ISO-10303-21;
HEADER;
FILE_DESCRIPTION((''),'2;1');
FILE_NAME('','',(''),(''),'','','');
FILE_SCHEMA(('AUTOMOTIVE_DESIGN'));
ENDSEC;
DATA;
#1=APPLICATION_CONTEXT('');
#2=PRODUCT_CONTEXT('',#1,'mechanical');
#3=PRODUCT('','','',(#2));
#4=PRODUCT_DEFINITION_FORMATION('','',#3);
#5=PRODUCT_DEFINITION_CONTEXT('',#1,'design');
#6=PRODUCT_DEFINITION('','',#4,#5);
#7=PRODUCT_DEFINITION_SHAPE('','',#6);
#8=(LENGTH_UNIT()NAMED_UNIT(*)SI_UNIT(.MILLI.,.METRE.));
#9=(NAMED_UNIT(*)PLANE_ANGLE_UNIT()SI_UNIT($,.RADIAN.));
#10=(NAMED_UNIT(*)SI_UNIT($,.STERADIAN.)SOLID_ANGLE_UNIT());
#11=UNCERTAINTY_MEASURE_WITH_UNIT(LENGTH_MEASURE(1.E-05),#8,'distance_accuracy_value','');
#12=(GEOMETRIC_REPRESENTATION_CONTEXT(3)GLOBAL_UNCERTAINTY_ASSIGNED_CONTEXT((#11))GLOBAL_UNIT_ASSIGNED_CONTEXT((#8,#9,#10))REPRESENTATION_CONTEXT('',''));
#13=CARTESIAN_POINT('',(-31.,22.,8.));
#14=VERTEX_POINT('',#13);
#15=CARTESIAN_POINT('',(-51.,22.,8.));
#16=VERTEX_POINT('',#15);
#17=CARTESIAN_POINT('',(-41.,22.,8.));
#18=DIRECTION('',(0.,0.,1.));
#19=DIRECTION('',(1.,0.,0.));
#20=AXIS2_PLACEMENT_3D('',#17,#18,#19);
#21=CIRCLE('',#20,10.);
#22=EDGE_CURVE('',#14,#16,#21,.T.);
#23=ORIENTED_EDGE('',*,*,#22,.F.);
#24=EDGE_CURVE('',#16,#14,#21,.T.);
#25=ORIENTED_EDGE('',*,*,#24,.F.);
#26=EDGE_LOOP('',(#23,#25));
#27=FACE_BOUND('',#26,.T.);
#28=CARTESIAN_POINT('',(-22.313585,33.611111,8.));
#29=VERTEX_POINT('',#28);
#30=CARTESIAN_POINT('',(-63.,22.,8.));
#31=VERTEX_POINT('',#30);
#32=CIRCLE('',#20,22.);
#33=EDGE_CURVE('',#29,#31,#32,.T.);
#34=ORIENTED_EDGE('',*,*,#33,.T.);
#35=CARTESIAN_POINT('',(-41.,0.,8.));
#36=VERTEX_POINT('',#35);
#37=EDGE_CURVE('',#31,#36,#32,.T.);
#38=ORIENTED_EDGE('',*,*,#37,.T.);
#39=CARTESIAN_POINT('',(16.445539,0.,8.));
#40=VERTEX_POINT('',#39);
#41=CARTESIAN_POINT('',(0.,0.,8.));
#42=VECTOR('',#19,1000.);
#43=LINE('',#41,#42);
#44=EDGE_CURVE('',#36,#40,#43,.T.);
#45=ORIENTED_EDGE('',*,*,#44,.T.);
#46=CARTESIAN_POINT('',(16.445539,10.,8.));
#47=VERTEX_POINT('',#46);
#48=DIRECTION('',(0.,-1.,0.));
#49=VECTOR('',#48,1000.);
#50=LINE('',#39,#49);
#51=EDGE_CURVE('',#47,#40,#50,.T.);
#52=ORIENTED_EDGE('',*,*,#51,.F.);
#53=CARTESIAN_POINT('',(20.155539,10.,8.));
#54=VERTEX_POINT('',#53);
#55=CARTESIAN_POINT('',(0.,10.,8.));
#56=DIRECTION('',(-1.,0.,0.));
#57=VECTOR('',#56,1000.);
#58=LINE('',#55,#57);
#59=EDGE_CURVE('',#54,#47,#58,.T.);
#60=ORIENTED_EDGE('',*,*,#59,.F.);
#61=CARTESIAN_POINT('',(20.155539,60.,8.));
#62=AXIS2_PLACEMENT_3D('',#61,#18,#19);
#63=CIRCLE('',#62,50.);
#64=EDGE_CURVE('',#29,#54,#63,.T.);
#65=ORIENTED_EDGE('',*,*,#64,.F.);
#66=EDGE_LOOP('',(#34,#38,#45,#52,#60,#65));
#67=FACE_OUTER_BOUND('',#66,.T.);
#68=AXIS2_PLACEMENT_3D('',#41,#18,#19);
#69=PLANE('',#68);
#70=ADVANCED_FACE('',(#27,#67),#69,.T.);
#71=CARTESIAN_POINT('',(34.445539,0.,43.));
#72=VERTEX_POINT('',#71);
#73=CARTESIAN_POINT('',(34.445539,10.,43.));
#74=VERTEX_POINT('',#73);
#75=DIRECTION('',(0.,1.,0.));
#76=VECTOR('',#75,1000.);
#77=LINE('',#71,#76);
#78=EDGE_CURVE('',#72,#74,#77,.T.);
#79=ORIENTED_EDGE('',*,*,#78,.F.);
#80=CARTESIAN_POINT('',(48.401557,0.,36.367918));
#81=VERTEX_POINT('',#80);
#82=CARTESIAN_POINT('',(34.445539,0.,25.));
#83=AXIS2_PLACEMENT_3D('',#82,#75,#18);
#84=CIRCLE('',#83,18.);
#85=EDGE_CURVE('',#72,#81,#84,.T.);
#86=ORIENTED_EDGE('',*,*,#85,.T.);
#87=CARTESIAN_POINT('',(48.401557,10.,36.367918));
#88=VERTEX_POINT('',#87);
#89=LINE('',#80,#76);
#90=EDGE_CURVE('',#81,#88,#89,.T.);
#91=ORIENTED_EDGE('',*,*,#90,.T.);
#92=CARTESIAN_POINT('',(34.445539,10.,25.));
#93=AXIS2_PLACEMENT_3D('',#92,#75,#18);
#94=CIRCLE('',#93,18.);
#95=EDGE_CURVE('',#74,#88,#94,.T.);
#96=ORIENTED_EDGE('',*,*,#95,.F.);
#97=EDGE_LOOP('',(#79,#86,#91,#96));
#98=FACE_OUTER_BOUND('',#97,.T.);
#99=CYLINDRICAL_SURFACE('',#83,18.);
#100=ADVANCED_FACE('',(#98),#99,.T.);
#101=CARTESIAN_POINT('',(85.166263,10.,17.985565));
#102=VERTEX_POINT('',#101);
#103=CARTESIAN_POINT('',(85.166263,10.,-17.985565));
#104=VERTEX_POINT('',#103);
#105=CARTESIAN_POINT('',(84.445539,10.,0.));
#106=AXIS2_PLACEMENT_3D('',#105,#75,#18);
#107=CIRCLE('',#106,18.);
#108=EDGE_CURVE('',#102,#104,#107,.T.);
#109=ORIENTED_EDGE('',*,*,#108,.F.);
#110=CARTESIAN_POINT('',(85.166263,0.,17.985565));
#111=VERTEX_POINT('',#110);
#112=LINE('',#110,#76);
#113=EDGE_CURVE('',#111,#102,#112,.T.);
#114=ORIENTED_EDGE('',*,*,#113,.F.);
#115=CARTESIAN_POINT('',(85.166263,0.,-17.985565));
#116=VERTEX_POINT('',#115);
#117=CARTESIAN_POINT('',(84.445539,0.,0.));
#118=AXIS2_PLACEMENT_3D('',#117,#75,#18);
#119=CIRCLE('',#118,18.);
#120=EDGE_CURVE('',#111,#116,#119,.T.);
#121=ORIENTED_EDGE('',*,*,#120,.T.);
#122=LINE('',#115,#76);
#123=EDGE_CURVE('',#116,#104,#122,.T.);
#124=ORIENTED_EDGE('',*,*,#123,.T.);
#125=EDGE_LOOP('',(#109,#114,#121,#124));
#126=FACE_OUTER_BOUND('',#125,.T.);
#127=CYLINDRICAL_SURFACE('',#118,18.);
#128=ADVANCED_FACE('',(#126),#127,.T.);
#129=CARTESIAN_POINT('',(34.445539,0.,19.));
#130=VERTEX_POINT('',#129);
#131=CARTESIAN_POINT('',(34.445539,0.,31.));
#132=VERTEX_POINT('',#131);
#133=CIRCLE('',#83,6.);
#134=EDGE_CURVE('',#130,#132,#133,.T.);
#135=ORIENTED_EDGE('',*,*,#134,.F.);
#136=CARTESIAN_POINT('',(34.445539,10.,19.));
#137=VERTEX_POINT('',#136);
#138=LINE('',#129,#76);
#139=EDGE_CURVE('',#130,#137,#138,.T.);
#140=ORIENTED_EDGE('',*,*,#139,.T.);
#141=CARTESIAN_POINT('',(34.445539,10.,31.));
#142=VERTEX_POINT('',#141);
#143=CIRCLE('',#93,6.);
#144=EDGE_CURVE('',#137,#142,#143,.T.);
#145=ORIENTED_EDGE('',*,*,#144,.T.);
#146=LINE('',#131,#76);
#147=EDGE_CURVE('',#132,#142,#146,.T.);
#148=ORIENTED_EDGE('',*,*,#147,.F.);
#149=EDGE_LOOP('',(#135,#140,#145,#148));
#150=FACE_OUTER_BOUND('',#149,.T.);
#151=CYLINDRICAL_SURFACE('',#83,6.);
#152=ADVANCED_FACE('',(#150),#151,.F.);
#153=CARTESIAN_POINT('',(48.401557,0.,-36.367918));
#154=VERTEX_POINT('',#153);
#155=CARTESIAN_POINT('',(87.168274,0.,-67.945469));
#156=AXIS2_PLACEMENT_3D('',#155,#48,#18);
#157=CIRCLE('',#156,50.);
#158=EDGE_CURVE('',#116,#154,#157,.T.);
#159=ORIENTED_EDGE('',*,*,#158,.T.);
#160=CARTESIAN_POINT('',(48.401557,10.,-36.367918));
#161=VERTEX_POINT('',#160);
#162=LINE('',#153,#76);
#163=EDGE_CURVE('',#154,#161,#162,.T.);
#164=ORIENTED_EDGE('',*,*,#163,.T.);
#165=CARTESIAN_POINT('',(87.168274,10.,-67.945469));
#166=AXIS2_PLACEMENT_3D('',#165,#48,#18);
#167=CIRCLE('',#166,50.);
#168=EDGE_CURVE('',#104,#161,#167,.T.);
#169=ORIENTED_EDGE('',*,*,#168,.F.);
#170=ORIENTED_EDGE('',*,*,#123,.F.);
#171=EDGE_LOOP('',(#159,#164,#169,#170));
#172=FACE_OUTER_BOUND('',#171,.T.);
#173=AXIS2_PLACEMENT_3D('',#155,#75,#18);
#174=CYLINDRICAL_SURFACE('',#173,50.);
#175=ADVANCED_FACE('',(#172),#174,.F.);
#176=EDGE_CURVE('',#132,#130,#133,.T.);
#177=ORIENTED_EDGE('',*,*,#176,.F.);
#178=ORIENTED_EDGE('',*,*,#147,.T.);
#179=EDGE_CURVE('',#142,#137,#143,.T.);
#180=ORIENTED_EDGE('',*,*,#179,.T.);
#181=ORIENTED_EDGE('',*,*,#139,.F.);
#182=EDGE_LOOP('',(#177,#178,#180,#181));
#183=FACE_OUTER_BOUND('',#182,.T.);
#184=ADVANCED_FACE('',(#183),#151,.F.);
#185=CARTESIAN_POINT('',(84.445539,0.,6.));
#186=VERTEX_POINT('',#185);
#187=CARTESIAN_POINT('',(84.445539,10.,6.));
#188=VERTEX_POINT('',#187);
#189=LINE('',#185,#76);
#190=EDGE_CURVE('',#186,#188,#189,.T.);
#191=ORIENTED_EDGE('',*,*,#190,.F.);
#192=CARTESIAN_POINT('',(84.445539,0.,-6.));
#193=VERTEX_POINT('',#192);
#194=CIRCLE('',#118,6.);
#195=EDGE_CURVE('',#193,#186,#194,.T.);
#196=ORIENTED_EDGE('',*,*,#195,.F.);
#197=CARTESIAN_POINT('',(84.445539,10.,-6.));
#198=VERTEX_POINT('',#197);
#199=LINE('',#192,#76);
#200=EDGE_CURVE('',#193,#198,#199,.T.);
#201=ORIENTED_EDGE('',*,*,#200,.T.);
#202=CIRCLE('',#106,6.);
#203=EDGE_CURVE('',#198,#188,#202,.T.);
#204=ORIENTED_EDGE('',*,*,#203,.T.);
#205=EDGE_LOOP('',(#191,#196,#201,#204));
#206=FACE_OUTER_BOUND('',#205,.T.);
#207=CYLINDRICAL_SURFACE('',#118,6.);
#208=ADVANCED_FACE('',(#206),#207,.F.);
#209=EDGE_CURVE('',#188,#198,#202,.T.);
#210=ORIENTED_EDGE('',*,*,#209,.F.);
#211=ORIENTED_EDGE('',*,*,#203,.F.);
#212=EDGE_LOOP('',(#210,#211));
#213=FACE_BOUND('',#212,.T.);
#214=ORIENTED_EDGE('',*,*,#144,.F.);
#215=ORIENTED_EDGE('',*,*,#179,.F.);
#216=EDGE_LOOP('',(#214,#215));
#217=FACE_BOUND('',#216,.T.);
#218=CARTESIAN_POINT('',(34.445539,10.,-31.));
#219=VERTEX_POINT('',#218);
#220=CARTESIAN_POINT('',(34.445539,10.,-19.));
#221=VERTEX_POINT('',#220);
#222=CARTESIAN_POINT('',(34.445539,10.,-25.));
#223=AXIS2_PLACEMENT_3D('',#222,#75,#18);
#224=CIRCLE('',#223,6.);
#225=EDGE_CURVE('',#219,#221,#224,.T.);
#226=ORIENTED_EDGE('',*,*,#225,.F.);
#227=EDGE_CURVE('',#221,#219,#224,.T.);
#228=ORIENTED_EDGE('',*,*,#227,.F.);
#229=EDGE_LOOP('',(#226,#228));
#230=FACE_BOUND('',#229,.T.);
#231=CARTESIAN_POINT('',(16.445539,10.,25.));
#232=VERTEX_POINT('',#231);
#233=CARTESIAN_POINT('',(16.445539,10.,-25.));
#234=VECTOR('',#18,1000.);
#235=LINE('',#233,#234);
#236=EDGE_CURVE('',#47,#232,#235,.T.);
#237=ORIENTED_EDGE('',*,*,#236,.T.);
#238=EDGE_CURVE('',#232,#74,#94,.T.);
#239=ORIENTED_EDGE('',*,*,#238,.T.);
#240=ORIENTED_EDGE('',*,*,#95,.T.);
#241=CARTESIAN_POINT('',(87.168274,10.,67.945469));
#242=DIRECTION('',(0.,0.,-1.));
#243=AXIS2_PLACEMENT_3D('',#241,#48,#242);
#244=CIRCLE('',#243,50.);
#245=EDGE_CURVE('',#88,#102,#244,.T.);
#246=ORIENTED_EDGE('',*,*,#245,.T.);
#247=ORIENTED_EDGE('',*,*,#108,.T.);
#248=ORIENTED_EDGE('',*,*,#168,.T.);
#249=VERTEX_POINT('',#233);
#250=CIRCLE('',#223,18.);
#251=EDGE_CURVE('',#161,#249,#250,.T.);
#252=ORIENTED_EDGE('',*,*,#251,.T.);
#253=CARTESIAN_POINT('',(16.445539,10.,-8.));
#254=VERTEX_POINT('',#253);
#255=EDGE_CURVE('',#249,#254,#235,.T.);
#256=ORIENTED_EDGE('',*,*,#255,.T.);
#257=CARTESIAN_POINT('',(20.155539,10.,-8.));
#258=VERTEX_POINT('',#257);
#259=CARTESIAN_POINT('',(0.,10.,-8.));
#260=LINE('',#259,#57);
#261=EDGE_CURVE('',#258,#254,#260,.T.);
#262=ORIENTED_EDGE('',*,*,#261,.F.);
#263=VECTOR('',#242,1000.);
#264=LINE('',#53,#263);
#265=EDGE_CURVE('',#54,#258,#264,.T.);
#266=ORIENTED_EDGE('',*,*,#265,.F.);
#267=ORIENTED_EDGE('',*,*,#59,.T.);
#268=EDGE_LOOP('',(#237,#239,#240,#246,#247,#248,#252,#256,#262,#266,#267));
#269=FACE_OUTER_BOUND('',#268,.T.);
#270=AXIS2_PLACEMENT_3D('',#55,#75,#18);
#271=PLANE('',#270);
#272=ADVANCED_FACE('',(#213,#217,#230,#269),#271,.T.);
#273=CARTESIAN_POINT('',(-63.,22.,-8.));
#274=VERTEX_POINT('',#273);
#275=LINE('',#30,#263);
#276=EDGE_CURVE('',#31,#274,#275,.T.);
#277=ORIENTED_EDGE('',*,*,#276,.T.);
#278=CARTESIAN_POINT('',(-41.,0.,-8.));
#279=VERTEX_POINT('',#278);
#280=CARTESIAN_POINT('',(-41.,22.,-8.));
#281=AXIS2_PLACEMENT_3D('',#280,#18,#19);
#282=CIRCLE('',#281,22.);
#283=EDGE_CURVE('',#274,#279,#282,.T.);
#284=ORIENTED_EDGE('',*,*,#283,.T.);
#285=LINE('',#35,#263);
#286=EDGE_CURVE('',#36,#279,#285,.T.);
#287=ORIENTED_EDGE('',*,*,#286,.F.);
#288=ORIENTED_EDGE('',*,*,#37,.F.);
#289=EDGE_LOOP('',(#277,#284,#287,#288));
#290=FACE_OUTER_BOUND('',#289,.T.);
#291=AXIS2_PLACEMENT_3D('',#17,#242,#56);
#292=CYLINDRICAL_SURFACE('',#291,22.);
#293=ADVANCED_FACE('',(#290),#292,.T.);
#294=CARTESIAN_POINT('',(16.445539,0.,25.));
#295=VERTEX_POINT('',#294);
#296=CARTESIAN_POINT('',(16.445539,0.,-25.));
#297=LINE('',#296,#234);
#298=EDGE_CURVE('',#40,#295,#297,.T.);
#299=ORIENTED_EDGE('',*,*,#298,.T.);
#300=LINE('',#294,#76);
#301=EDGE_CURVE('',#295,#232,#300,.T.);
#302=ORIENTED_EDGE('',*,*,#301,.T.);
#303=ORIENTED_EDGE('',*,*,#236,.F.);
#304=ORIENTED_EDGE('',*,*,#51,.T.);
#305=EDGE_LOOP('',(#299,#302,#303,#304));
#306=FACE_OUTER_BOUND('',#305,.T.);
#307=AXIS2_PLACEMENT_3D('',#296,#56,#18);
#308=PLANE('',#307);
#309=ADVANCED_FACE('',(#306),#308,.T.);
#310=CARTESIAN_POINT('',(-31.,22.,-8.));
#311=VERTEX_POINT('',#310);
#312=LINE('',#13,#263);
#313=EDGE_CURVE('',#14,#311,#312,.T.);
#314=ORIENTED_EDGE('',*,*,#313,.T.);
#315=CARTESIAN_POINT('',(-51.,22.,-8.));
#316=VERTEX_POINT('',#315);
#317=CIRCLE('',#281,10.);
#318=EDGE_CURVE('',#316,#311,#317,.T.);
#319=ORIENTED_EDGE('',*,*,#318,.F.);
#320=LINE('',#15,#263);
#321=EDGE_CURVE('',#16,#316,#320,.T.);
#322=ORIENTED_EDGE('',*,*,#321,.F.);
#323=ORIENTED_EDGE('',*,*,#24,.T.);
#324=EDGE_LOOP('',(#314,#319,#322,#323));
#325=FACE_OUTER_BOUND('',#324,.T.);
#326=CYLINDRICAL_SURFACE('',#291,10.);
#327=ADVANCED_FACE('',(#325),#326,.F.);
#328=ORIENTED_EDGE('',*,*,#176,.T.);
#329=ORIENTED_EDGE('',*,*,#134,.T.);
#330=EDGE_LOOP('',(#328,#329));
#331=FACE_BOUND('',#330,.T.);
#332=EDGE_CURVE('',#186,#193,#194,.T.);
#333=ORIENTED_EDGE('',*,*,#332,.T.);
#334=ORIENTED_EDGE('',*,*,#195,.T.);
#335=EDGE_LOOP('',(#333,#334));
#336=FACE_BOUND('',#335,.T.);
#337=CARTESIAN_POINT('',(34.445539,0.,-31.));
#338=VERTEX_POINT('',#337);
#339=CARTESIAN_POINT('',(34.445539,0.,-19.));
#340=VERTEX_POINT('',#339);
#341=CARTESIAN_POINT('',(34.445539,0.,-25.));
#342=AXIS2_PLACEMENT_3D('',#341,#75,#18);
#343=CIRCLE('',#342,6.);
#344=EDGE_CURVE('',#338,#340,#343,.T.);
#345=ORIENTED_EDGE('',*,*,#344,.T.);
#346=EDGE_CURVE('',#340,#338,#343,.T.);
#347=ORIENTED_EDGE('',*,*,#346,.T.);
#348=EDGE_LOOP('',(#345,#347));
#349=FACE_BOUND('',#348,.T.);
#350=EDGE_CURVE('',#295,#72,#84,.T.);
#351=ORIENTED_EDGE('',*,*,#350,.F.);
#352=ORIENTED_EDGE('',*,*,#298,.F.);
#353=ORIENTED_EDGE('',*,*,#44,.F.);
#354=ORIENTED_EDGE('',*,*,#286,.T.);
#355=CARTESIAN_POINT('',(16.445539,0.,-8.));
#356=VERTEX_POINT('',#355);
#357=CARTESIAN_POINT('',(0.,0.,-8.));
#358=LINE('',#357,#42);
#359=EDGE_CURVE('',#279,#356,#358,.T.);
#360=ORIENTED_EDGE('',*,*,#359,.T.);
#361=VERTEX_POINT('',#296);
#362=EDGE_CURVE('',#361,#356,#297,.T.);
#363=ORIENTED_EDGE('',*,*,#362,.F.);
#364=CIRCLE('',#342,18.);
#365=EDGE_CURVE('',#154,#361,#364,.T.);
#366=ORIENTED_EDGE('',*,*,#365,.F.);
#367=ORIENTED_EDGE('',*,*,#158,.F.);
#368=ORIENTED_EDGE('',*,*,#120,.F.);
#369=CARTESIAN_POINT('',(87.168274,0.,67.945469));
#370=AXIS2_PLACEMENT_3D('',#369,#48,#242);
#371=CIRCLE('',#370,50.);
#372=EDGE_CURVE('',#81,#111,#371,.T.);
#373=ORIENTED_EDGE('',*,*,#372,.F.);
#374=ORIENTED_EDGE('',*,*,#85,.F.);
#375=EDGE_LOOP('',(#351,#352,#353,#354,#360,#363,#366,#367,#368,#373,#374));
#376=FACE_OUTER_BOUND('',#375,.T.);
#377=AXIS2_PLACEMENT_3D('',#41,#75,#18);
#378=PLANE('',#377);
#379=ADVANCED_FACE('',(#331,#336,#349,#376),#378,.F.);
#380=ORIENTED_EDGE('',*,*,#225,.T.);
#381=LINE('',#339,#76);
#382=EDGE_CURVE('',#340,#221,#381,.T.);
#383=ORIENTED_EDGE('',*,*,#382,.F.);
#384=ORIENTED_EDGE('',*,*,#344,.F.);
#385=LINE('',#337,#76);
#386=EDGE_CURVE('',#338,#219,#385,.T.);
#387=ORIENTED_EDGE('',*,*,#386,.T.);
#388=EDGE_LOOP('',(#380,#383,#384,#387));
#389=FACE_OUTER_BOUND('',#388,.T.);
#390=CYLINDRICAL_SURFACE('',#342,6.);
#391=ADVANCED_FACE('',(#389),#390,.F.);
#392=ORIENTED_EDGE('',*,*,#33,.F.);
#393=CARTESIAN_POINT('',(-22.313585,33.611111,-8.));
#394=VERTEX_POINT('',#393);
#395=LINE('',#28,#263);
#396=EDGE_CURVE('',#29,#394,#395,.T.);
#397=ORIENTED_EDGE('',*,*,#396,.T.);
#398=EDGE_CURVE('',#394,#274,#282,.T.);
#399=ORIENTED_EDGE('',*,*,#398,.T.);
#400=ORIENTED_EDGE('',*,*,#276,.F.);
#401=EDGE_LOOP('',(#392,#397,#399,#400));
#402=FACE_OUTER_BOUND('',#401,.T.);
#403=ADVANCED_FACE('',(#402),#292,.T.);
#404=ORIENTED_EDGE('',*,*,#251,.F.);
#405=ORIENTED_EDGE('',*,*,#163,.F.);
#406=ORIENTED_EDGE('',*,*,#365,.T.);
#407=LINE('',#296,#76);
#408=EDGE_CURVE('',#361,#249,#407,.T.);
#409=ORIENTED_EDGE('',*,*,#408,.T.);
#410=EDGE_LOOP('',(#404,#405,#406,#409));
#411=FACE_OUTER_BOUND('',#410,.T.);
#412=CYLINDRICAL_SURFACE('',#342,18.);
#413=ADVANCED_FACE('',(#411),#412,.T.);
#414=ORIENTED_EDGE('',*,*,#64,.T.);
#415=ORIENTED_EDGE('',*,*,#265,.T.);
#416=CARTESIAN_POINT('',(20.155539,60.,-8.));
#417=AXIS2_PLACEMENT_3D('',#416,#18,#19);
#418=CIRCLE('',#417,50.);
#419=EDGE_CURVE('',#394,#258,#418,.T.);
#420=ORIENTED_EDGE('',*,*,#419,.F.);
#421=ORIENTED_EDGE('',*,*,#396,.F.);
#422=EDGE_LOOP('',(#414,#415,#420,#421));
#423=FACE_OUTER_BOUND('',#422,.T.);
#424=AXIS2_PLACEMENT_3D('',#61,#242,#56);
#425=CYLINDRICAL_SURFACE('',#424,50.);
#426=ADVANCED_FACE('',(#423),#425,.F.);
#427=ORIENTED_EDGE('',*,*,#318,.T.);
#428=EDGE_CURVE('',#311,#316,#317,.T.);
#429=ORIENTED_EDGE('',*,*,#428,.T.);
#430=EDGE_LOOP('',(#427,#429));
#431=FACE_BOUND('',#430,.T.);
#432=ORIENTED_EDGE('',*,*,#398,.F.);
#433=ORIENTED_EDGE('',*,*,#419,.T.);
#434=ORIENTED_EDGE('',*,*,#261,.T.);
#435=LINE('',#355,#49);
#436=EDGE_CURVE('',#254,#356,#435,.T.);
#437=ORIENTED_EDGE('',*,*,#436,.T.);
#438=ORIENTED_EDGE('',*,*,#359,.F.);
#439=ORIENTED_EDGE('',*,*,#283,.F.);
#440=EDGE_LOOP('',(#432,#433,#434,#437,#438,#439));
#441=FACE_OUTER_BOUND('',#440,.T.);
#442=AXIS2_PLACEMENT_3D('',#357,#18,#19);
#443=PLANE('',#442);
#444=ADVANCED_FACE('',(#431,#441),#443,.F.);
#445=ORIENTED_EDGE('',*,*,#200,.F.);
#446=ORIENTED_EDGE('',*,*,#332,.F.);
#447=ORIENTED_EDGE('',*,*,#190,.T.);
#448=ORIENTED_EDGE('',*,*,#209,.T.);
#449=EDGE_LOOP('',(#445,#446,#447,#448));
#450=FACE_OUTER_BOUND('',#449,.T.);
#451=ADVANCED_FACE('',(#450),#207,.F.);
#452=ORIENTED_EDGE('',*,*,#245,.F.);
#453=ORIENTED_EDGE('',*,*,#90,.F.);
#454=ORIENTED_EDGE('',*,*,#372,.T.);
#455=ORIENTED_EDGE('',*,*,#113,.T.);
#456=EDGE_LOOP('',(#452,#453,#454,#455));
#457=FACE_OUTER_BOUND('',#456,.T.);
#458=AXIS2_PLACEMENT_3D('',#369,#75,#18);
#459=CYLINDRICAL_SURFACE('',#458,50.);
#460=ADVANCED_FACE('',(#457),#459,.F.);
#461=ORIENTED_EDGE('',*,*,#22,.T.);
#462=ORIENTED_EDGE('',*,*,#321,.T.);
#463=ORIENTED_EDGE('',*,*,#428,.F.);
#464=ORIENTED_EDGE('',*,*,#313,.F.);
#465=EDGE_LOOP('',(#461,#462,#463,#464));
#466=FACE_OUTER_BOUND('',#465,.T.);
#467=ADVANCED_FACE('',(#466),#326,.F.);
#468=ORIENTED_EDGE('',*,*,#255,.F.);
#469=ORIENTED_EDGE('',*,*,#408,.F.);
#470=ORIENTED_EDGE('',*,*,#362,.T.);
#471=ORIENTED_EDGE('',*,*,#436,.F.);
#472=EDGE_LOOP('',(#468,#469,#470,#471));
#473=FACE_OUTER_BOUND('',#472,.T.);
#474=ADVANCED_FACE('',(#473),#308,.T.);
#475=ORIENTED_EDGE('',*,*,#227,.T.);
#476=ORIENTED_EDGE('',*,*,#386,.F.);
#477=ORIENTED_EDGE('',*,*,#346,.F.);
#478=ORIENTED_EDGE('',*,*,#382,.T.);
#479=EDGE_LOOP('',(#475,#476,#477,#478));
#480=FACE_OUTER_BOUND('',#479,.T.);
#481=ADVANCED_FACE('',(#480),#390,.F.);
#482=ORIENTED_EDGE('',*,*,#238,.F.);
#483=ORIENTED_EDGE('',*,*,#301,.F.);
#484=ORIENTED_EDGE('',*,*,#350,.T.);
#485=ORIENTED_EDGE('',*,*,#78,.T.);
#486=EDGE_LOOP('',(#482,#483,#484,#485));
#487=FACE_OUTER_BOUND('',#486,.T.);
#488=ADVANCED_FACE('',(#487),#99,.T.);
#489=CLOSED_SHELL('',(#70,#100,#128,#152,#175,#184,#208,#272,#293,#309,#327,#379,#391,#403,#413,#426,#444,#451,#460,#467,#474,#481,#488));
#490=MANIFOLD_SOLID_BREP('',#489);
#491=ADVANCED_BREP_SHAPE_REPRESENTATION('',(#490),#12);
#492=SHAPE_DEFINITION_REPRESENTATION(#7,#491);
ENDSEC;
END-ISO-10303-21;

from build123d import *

# Parameters (mm, degrees)
ARM_PROFILE_SKETCH_R     = 10
ARM_BODY_DEPTH           = 8
MOUNTING_FLANGE_SKETCH_R = 6
MOUNTING_FLANGE_DEPTH    = 10
TRIM_CUT_SKETCH_R        = 6
TRIM_CUT_DEPTH           = 117.189881419


with BuildPart() as part:
    # Arm Profile Sketch → Arm Body (new, symmetric)
    with BuildSketch(Plane.XY):
        with BuildLine():
            Line((-41, 0), (86, 0))
            Line((86, 0), (86, 10))
            Line((86, 10), (20.155539406, 10))
            ThreePointArc((20.155539406, 10), (-4.14009349, 16.299631326), (-22.313585182, 33.611111111))
            ThreePointArc((-22.313585182, 33.611111111), (-60.228162216, 32.690078474), (-41, 0))
        make_face()
        with Locations((-41, 22)):
            Circle(ARM_PROFILE_SKETCH_R, mode=Mode.SUBTRACT)
    extrude(amount=ARM_BODY_DEPTH, both=True)

    # Mounting Flange Sketch → Mounting Flange (add)
    with BuildSketch(Plane(origin=(0, 10, 0), x_dir=(1, 0, 0), z_dir=(0, 1, 0))):
        with BuildLine():
            Line((16.445539406, 25), (16.445539406, -25))
            ThreePointArc((16.445539406, -25), (28.412643024, -41.958896227), (48.401557323, -36.367918187))
            ThreePointArc((48.401557323, -36.367918187), (64.807593984, -23.224109156), (85.166263205, -17.985565246))
            ThreePointArc((85.166263205, -17.985565246), (102.445539406, 0), (85.166263205, 17.985565246))
            ThreePointArc((85.166263205, 17.985565246), (64.807593984, 23.224109156), (48.401557323, 36.367918187))
            ThreePointArc((48.401557323, 36.367918187), (28.412643024, 41.958896227), (16.445539406, 25))
        make_face()
        with Locations((84.445539406, 0)):
            Circle(MOUNTING_FLANGE_SKETCH_R, mode=Mode.SUBTRACT)
        with Locations(Location((34.445539406, 25, 0), (0, 0, 270))):
            Circle(MOUNTING_FLANGE_SKETCH_R, mode=Mode.SUBTRACT)
        with Locations(Location((34.445539406, -25, 0), (0, 0, 270))):
            Circle(MOUNTING_FLANGE_SKETCH_R, mode=Mode.SUBTRACT)
    extrude(amount=-MOUNTING_FLANGE_DEPTH)

    # Trim Cut Sketch → Trim Cut (cut, through all)
    with BuildSketch(Plane(origin=(0, 10, 0), x_dir=(1, 0, 0), z_dir=(0, 1, 0))):
        with Locations(Location((84.445539406, 0, 0), (0, 0, 270))):
            Circle(TRIM_CUT_SKETCH_R)
    extrude(amount=-TRIM_CUT_DEPTH, mode=Mode.SUBTRACT)


solid = part.part
